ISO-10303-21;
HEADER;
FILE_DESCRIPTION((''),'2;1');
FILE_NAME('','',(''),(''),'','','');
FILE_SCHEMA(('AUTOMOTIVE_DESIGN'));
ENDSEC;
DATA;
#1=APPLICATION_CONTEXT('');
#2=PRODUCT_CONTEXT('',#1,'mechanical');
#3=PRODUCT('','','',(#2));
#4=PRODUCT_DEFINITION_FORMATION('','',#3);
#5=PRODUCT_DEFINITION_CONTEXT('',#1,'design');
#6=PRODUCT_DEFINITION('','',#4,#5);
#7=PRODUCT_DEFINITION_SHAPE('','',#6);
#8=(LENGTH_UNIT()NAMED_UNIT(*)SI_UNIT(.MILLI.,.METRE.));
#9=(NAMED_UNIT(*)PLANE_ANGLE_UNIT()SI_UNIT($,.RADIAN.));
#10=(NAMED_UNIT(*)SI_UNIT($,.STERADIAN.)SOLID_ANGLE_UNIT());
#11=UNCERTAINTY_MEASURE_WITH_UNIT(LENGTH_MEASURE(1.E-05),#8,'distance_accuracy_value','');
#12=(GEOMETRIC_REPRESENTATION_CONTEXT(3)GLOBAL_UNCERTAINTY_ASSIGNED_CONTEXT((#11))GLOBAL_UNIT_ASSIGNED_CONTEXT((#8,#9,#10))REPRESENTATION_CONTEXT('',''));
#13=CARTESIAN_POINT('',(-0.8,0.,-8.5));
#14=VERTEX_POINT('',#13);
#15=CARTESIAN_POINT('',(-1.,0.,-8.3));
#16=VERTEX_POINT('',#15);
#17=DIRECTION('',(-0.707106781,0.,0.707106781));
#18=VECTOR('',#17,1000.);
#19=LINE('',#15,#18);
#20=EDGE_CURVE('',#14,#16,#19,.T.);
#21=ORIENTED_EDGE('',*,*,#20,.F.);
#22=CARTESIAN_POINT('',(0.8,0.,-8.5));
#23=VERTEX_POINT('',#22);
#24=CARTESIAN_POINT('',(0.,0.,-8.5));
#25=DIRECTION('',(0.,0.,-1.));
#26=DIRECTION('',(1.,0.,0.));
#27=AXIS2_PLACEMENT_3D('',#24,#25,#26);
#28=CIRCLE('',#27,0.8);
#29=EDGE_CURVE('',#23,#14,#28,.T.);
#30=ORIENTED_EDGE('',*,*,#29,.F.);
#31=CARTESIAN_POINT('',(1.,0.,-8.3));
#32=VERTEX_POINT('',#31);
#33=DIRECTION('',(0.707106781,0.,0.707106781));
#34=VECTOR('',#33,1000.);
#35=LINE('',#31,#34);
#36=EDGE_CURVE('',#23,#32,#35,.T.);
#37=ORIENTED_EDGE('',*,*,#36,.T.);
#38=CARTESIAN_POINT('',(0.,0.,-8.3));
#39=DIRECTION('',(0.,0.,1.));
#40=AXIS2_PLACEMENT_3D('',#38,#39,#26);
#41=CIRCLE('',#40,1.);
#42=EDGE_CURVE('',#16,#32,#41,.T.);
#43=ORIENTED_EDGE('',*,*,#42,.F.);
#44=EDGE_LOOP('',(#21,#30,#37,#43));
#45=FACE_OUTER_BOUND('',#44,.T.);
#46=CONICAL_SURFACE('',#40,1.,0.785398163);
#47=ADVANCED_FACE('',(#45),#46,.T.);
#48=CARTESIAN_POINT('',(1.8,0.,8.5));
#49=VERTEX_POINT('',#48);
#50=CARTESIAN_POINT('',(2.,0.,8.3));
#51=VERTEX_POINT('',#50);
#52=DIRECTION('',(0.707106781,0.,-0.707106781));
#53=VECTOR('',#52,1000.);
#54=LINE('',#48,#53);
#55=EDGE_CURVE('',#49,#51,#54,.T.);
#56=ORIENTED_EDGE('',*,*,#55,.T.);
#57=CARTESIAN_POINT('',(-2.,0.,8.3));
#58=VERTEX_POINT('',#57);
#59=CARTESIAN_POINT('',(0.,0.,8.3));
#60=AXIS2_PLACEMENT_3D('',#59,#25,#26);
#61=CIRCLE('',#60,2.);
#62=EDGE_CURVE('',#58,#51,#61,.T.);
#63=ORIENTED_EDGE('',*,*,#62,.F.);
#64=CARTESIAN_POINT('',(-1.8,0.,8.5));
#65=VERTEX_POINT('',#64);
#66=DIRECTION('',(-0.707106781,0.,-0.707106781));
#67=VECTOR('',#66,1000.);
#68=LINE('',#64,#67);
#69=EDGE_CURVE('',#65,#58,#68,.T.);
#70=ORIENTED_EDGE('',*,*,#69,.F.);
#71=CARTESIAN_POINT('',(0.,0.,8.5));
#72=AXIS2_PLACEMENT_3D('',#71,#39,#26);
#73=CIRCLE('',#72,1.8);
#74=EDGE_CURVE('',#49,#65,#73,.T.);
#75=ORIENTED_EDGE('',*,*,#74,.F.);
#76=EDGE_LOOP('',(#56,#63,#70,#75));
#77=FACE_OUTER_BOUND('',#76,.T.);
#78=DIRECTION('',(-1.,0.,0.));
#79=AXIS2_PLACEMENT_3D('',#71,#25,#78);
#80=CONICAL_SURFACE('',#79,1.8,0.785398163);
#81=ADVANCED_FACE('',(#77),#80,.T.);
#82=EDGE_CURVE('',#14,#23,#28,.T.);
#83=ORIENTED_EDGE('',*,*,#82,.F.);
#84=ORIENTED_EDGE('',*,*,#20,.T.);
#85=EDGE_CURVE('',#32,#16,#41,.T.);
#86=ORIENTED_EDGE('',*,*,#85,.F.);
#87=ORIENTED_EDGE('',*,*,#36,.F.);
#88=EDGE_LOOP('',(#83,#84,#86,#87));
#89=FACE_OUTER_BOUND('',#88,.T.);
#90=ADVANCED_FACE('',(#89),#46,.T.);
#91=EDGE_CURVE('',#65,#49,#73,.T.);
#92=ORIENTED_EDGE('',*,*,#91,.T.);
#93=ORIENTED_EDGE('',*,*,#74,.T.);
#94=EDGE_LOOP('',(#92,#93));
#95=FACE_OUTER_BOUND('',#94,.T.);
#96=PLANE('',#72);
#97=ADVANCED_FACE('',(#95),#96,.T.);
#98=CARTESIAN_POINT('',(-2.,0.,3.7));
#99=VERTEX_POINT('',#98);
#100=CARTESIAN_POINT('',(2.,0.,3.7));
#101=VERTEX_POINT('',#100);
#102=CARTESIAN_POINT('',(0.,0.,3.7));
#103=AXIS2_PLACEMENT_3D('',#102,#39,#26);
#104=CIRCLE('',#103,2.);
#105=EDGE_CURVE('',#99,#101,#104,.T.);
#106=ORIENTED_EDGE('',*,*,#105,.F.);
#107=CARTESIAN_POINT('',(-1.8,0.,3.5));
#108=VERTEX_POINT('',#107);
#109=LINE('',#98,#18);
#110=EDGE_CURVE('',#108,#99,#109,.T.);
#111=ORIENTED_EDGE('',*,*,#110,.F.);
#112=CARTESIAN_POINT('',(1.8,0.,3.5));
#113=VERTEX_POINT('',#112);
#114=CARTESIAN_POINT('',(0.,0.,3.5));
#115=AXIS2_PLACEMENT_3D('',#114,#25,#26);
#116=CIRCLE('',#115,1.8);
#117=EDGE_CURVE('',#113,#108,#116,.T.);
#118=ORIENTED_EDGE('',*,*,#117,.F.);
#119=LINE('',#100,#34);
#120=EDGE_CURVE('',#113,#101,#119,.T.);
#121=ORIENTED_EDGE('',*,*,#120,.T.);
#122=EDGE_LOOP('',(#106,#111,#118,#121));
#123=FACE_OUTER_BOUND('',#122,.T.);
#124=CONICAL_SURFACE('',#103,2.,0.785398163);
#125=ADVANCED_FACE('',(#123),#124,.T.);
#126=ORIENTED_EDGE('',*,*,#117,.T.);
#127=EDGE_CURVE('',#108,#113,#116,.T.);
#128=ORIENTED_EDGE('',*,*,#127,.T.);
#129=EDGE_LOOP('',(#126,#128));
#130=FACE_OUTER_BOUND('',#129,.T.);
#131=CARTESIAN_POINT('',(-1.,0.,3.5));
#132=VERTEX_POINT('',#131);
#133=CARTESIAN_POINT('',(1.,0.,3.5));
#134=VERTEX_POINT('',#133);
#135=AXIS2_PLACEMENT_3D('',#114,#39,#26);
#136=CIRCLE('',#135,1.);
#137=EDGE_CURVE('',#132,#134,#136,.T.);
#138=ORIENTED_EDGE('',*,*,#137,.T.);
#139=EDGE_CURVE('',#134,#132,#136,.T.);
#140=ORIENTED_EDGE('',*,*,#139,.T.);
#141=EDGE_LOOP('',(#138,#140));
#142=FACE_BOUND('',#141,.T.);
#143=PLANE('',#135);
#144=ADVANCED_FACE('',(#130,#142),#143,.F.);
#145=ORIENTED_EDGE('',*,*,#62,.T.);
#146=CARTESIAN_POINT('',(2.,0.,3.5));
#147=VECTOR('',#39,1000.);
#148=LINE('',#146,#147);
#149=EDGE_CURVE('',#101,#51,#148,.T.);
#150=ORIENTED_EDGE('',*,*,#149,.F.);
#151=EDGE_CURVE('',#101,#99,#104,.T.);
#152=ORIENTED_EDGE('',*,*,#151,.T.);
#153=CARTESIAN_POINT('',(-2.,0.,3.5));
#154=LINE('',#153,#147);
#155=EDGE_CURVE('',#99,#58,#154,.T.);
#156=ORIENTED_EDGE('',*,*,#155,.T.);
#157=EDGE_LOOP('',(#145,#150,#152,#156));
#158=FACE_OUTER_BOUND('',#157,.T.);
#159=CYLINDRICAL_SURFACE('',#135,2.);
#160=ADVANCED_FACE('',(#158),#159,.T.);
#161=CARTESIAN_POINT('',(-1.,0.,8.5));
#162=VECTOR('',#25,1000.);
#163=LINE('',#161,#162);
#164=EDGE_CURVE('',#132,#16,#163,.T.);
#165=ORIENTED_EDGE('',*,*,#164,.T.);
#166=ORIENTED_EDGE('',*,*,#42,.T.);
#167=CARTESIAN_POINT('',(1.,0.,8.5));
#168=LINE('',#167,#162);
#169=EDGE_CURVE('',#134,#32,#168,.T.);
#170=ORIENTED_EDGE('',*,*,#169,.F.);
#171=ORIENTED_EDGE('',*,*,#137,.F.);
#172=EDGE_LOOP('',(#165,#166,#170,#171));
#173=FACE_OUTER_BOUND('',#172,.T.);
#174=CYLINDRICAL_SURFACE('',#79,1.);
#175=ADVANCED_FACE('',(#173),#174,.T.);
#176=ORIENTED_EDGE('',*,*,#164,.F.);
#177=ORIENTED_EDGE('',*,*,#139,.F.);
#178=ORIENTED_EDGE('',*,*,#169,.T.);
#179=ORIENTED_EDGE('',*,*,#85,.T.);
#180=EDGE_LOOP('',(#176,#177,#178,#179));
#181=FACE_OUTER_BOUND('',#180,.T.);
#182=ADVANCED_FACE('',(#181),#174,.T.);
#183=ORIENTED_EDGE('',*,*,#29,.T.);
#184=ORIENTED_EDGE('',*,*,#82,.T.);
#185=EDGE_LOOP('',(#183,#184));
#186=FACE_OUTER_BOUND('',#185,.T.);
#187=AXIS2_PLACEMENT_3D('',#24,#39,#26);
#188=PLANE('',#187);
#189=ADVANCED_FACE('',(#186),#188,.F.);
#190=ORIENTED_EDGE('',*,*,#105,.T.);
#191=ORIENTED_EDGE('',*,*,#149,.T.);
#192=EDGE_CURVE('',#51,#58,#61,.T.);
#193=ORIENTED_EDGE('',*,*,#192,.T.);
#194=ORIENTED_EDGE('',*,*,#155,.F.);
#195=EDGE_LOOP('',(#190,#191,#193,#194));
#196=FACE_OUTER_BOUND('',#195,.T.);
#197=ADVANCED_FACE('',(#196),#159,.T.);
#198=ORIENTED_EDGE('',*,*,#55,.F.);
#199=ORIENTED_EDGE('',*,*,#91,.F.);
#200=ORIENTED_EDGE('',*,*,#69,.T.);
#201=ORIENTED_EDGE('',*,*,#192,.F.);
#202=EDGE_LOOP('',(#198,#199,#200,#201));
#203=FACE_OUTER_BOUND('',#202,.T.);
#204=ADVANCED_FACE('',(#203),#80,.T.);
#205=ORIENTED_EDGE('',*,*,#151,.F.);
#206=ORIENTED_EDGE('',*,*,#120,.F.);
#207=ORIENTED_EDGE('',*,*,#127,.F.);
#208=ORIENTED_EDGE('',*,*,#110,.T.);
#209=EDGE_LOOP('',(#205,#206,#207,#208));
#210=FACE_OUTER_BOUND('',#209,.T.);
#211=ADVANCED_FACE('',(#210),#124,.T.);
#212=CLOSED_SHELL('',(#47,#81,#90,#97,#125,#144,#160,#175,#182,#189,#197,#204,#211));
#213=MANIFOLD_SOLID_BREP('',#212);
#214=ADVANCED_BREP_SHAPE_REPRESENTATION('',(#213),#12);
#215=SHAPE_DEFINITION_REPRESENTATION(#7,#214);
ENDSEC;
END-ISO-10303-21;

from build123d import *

# Parameters (mm, degrees)
SKETCH1_R           = 1
BOSS_EXTRUDE1_DEPTH = 8.5
SKETCH2_R           = 2
BOSS_EXTRUDE2_DEPTH = 5
CHAMFER1_SIZE       = 0.2


with BuildPart() as part:
    # Sketch1 → Boss-Extrude1 (new, symmetric)
    with BuildSketch(Plane.XY):
        Circle(SKETCH1_R)
    extrude(amount=BOSS_EXTRUDE1_DEPTH, both=True)

    # Sketch2 → Boss-Extrude2 (add)
    with BuildSketch(Plane.XY.offset(8.5)):
        Circle(SKETCH2_R)
    extrude(amount=-BOSS_EXTRUDE2_DEPTH)

    # Chamfer1
    chamfer1_edges = [part.edges().sort_by_distance(p)[0] for p in [
        (-1, 0, -8.5),
        (-2, 0, 8.5),
        (-2, 0, 3.5),
    ]]
    chamfer(chamfer1_edges, length=CHAMFER1_SIZE)


solid = part.part
